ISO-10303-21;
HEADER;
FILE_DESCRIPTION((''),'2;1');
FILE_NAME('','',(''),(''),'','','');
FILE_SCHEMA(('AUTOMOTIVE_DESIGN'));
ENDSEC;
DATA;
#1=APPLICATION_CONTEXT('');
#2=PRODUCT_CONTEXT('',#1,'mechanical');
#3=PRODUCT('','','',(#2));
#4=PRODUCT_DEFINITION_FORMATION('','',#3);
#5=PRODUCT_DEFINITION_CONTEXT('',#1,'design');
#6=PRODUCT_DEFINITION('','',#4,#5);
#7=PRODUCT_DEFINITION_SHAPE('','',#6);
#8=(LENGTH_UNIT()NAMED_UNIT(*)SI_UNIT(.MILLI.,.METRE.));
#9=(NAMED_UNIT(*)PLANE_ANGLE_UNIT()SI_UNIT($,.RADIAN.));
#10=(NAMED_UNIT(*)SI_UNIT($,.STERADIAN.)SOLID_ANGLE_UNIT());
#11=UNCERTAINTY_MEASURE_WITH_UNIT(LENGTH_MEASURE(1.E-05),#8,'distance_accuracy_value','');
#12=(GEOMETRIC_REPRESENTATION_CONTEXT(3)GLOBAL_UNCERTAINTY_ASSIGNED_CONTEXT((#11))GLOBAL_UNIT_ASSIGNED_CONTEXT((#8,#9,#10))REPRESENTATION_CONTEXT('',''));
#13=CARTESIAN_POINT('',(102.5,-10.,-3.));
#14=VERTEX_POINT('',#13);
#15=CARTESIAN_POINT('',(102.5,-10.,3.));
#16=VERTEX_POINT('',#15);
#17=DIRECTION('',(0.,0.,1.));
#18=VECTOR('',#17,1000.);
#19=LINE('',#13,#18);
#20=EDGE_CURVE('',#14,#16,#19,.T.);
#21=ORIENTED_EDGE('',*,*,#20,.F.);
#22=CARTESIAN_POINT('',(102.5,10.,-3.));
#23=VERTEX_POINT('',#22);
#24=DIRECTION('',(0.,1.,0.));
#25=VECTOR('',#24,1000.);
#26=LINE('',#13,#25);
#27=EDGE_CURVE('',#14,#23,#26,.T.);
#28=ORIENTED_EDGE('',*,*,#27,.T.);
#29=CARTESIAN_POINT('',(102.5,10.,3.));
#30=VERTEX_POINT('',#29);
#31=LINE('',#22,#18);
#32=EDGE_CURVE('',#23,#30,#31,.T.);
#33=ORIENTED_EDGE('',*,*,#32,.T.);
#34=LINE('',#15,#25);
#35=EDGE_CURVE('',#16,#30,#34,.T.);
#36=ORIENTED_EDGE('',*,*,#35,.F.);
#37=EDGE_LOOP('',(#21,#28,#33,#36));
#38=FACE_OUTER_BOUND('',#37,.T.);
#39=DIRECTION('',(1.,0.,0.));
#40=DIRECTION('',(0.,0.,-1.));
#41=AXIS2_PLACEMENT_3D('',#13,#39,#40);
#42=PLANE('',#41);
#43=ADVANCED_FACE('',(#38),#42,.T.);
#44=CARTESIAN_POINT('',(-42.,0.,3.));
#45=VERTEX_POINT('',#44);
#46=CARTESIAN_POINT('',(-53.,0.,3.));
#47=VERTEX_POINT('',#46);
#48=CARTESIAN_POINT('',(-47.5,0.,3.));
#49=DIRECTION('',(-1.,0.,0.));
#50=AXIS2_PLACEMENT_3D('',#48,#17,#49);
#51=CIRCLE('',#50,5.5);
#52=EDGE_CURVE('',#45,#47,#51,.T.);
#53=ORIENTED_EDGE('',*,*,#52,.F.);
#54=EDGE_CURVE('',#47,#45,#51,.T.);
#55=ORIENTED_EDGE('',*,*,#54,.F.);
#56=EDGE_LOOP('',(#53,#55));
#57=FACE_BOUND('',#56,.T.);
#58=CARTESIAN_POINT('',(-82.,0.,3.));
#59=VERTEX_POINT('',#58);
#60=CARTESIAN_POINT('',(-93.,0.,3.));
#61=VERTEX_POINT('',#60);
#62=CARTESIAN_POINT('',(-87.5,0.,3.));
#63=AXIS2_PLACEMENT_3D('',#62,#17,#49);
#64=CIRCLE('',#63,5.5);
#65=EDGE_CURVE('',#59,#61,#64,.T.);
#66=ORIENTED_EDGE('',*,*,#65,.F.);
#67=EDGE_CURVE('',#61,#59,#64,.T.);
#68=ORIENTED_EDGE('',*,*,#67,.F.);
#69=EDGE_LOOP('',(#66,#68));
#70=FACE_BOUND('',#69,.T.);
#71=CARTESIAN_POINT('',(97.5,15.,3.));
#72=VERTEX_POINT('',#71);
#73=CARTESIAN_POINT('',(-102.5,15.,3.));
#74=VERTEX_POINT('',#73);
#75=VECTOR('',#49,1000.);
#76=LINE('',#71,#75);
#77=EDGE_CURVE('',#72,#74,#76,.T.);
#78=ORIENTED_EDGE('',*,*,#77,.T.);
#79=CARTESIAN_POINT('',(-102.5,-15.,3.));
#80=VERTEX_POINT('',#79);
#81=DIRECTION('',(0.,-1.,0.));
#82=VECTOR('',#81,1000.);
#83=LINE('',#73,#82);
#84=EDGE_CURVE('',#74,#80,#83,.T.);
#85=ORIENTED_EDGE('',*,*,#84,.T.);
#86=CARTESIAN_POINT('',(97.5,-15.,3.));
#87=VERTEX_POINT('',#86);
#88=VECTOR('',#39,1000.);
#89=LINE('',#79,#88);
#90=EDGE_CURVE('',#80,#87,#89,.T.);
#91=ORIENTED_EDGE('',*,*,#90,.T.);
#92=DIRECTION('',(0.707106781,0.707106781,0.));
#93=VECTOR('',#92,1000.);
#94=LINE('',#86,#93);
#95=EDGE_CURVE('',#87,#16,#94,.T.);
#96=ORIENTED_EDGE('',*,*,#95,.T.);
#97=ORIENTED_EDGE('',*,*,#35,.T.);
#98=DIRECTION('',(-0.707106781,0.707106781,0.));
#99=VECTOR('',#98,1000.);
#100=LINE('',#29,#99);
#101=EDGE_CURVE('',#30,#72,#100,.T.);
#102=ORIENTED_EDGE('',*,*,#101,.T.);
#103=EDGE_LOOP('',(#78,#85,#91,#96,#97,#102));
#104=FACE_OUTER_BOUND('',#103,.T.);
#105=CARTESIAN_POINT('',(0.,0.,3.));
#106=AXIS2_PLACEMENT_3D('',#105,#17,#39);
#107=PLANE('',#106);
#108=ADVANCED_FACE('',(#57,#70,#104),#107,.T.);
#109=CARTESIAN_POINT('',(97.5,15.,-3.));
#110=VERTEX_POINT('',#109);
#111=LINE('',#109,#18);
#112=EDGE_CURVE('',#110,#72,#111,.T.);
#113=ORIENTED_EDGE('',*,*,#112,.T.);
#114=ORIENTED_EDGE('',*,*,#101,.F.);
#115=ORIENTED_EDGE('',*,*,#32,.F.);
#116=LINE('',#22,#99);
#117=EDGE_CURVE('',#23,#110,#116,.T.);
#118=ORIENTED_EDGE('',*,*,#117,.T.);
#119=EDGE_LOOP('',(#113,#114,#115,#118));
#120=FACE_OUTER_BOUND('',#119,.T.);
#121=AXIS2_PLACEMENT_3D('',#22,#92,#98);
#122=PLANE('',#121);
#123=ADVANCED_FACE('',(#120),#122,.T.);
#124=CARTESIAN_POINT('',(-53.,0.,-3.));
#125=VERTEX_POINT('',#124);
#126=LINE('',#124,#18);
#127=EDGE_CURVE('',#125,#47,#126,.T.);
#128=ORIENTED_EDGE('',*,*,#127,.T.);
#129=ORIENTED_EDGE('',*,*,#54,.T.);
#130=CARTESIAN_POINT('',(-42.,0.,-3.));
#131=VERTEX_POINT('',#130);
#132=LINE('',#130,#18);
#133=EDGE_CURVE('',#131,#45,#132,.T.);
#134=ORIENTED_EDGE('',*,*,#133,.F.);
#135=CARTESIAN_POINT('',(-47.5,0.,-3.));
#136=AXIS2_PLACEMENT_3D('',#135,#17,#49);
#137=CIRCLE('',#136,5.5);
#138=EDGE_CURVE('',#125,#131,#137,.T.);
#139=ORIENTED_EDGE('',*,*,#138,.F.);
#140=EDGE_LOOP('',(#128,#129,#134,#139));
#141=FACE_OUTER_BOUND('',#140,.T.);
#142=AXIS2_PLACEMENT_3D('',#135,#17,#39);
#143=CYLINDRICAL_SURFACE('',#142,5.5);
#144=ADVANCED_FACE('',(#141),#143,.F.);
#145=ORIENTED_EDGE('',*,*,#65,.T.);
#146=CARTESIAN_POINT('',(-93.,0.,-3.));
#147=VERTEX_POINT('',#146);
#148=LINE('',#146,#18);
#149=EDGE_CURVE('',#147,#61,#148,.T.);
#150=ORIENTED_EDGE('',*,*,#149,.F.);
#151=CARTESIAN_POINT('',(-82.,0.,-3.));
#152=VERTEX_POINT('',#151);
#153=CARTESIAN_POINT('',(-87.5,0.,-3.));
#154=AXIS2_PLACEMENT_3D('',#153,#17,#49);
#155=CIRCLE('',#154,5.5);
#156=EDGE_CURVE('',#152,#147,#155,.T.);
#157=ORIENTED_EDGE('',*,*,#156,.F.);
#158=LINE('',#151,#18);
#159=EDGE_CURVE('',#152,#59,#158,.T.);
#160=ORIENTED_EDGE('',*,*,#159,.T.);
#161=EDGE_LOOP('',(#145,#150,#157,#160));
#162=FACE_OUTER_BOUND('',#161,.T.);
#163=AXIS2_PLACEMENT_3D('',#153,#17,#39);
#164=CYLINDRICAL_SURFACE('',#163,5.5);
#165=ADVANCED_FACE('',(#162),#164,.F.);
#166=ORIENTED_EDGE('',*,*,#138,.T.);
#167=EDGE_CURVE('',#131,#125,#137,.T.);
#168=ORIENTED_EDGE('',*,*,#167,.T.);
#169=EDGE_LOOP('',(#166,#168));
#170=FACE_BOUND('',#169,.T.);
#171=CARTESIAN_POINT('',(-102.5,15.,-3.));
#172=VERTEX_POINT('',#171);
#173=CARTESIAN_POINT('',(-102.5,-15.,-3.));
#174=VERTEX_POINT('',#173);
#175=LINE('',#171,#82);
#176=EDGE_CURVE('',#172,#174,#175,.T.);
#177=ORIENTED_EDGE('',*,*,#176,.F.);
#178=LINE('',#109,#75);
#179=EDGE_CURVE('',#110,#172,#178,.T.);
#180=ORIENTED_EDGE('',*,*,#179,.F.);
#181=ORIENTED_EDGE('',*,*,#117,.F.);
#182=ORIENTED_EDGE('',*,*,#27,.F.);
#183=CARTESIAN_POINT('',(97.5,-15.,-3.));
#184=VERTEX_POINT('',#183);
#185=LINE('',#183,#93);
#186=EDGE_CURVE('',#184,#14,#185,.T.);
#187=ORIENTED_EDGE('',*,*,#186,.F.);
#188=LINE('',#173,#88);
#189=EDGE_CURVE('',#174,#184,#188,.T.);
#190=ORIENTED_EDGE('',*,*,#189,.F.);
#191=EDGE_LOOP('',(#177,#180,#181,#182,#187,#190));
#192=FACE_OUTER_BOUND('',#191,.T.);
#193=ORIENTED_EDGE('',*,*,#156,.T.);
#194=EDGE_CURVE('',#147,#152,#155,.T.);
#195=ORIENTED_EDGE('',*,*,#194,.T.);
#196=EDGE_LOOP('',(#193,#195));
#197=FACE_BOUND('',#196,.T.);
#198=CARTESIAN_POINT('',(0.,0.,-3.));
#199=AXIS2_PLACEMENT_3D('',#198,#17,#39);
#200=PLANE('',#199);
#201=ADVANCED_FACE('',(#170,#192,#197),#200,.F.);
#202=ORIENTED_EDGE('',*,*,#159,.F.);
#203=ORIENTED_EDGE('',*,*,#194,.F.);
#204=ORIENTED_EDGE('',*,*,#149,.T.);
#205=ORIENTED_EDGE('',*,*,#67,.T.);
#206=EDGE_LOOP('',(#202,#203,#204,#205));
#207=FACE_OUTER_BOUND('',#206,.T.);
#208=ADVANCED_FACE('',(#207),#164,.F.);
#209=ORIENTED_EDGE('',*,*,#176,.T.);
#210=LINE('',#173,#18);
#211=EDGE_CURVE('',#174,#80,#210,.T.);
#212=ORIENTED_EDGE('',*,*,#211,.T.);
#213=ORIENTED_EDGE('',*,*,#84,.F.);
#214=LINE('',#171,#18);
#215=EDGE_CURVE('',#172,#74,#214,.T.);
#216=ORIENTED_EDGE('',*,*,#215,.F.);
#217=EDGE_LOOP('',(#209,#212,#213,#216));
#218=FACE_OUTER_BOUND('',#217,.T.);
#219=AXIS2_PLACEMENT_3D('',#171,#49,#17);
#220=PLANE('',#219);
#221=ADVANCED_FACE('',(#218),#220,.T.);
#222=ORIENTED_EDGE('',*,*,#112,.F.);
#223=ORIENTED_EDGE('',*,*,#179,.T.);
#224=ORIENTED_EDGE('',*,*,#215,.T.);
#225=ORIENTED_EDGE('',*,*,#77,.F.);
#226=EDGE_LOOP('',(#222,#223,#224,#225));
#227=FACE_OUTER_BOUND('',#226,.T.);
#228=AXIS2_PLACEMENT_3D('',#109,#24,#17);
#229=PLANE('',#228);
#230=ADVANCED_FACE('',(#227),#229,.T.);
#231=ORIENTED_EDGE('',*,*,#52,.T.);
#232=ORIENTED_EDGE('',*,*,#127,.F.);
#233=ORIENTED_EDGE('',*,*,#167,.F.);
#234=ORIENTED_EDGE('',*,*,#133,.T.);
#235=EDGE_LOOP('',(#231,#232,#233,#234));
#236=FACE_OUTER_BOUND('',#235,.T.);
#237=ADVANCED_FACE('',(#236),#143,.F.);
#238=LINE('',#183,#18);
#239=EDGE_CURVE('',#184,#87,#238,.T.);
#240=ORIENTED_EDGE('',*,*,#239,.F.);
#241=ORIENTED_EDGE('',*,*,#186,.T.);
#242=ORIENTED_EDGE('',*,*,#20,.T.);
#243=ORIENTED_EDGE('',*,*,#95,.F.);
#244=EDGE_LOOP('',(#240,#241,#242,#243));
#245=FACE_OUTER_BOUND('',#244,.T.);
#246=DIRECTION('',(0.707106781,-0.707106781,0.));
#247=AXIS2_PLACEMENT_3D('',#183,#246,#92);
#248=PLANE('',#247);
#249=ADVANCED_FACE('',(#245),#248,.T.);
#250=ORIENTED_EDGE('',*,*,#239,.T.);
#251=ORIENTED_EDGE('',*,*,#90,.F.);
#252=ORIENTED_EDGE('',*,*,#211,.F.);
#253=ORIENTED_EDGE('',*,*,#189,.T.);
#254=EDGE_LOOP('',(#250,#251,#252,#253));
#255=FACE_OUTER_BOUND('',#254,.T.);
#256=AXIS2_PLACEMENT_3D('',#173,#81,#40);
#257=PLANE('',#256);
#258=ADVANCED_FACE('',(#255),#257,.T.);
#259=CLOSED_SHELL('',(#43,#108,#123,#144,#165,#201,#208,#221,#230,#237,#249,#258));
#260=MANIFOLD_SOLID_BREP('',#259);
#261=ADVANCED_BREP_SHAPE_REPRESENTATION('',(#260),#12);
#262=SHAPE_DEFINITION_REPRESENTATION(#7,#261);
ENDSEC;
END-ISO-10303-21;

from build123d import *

# Parameters (mm, degrees)
SKETCH1_R           = 5.5
BOSS_EXTRUDE1_DEPTH = 6


with BuildPart() as part:
    # Sketch1 → Boss-Extrude1 (new body)
    with BuildSketch(Plane.XY.offset(3)):
        Polygon((102.5, -10), (102.5, 10), (97.5, 15), (-102.5, 15), (-102.5, -15), (97.5, -15), align=None)
        with Locations(Location((-87.5, 0, 0), (0, 0, 180))):
            Circle(SKETCH1_R, mode=Mode.SUBTRACT)
        with Locations(Location((-47.5, 0, 0), (0, 0, 180))):
            Circle(SKETCH1_R, mode=Mode.SUBTRACT)
    extrude(amount=-BOSS_EXTRUDE1_DEPTH)


solid = part.part
